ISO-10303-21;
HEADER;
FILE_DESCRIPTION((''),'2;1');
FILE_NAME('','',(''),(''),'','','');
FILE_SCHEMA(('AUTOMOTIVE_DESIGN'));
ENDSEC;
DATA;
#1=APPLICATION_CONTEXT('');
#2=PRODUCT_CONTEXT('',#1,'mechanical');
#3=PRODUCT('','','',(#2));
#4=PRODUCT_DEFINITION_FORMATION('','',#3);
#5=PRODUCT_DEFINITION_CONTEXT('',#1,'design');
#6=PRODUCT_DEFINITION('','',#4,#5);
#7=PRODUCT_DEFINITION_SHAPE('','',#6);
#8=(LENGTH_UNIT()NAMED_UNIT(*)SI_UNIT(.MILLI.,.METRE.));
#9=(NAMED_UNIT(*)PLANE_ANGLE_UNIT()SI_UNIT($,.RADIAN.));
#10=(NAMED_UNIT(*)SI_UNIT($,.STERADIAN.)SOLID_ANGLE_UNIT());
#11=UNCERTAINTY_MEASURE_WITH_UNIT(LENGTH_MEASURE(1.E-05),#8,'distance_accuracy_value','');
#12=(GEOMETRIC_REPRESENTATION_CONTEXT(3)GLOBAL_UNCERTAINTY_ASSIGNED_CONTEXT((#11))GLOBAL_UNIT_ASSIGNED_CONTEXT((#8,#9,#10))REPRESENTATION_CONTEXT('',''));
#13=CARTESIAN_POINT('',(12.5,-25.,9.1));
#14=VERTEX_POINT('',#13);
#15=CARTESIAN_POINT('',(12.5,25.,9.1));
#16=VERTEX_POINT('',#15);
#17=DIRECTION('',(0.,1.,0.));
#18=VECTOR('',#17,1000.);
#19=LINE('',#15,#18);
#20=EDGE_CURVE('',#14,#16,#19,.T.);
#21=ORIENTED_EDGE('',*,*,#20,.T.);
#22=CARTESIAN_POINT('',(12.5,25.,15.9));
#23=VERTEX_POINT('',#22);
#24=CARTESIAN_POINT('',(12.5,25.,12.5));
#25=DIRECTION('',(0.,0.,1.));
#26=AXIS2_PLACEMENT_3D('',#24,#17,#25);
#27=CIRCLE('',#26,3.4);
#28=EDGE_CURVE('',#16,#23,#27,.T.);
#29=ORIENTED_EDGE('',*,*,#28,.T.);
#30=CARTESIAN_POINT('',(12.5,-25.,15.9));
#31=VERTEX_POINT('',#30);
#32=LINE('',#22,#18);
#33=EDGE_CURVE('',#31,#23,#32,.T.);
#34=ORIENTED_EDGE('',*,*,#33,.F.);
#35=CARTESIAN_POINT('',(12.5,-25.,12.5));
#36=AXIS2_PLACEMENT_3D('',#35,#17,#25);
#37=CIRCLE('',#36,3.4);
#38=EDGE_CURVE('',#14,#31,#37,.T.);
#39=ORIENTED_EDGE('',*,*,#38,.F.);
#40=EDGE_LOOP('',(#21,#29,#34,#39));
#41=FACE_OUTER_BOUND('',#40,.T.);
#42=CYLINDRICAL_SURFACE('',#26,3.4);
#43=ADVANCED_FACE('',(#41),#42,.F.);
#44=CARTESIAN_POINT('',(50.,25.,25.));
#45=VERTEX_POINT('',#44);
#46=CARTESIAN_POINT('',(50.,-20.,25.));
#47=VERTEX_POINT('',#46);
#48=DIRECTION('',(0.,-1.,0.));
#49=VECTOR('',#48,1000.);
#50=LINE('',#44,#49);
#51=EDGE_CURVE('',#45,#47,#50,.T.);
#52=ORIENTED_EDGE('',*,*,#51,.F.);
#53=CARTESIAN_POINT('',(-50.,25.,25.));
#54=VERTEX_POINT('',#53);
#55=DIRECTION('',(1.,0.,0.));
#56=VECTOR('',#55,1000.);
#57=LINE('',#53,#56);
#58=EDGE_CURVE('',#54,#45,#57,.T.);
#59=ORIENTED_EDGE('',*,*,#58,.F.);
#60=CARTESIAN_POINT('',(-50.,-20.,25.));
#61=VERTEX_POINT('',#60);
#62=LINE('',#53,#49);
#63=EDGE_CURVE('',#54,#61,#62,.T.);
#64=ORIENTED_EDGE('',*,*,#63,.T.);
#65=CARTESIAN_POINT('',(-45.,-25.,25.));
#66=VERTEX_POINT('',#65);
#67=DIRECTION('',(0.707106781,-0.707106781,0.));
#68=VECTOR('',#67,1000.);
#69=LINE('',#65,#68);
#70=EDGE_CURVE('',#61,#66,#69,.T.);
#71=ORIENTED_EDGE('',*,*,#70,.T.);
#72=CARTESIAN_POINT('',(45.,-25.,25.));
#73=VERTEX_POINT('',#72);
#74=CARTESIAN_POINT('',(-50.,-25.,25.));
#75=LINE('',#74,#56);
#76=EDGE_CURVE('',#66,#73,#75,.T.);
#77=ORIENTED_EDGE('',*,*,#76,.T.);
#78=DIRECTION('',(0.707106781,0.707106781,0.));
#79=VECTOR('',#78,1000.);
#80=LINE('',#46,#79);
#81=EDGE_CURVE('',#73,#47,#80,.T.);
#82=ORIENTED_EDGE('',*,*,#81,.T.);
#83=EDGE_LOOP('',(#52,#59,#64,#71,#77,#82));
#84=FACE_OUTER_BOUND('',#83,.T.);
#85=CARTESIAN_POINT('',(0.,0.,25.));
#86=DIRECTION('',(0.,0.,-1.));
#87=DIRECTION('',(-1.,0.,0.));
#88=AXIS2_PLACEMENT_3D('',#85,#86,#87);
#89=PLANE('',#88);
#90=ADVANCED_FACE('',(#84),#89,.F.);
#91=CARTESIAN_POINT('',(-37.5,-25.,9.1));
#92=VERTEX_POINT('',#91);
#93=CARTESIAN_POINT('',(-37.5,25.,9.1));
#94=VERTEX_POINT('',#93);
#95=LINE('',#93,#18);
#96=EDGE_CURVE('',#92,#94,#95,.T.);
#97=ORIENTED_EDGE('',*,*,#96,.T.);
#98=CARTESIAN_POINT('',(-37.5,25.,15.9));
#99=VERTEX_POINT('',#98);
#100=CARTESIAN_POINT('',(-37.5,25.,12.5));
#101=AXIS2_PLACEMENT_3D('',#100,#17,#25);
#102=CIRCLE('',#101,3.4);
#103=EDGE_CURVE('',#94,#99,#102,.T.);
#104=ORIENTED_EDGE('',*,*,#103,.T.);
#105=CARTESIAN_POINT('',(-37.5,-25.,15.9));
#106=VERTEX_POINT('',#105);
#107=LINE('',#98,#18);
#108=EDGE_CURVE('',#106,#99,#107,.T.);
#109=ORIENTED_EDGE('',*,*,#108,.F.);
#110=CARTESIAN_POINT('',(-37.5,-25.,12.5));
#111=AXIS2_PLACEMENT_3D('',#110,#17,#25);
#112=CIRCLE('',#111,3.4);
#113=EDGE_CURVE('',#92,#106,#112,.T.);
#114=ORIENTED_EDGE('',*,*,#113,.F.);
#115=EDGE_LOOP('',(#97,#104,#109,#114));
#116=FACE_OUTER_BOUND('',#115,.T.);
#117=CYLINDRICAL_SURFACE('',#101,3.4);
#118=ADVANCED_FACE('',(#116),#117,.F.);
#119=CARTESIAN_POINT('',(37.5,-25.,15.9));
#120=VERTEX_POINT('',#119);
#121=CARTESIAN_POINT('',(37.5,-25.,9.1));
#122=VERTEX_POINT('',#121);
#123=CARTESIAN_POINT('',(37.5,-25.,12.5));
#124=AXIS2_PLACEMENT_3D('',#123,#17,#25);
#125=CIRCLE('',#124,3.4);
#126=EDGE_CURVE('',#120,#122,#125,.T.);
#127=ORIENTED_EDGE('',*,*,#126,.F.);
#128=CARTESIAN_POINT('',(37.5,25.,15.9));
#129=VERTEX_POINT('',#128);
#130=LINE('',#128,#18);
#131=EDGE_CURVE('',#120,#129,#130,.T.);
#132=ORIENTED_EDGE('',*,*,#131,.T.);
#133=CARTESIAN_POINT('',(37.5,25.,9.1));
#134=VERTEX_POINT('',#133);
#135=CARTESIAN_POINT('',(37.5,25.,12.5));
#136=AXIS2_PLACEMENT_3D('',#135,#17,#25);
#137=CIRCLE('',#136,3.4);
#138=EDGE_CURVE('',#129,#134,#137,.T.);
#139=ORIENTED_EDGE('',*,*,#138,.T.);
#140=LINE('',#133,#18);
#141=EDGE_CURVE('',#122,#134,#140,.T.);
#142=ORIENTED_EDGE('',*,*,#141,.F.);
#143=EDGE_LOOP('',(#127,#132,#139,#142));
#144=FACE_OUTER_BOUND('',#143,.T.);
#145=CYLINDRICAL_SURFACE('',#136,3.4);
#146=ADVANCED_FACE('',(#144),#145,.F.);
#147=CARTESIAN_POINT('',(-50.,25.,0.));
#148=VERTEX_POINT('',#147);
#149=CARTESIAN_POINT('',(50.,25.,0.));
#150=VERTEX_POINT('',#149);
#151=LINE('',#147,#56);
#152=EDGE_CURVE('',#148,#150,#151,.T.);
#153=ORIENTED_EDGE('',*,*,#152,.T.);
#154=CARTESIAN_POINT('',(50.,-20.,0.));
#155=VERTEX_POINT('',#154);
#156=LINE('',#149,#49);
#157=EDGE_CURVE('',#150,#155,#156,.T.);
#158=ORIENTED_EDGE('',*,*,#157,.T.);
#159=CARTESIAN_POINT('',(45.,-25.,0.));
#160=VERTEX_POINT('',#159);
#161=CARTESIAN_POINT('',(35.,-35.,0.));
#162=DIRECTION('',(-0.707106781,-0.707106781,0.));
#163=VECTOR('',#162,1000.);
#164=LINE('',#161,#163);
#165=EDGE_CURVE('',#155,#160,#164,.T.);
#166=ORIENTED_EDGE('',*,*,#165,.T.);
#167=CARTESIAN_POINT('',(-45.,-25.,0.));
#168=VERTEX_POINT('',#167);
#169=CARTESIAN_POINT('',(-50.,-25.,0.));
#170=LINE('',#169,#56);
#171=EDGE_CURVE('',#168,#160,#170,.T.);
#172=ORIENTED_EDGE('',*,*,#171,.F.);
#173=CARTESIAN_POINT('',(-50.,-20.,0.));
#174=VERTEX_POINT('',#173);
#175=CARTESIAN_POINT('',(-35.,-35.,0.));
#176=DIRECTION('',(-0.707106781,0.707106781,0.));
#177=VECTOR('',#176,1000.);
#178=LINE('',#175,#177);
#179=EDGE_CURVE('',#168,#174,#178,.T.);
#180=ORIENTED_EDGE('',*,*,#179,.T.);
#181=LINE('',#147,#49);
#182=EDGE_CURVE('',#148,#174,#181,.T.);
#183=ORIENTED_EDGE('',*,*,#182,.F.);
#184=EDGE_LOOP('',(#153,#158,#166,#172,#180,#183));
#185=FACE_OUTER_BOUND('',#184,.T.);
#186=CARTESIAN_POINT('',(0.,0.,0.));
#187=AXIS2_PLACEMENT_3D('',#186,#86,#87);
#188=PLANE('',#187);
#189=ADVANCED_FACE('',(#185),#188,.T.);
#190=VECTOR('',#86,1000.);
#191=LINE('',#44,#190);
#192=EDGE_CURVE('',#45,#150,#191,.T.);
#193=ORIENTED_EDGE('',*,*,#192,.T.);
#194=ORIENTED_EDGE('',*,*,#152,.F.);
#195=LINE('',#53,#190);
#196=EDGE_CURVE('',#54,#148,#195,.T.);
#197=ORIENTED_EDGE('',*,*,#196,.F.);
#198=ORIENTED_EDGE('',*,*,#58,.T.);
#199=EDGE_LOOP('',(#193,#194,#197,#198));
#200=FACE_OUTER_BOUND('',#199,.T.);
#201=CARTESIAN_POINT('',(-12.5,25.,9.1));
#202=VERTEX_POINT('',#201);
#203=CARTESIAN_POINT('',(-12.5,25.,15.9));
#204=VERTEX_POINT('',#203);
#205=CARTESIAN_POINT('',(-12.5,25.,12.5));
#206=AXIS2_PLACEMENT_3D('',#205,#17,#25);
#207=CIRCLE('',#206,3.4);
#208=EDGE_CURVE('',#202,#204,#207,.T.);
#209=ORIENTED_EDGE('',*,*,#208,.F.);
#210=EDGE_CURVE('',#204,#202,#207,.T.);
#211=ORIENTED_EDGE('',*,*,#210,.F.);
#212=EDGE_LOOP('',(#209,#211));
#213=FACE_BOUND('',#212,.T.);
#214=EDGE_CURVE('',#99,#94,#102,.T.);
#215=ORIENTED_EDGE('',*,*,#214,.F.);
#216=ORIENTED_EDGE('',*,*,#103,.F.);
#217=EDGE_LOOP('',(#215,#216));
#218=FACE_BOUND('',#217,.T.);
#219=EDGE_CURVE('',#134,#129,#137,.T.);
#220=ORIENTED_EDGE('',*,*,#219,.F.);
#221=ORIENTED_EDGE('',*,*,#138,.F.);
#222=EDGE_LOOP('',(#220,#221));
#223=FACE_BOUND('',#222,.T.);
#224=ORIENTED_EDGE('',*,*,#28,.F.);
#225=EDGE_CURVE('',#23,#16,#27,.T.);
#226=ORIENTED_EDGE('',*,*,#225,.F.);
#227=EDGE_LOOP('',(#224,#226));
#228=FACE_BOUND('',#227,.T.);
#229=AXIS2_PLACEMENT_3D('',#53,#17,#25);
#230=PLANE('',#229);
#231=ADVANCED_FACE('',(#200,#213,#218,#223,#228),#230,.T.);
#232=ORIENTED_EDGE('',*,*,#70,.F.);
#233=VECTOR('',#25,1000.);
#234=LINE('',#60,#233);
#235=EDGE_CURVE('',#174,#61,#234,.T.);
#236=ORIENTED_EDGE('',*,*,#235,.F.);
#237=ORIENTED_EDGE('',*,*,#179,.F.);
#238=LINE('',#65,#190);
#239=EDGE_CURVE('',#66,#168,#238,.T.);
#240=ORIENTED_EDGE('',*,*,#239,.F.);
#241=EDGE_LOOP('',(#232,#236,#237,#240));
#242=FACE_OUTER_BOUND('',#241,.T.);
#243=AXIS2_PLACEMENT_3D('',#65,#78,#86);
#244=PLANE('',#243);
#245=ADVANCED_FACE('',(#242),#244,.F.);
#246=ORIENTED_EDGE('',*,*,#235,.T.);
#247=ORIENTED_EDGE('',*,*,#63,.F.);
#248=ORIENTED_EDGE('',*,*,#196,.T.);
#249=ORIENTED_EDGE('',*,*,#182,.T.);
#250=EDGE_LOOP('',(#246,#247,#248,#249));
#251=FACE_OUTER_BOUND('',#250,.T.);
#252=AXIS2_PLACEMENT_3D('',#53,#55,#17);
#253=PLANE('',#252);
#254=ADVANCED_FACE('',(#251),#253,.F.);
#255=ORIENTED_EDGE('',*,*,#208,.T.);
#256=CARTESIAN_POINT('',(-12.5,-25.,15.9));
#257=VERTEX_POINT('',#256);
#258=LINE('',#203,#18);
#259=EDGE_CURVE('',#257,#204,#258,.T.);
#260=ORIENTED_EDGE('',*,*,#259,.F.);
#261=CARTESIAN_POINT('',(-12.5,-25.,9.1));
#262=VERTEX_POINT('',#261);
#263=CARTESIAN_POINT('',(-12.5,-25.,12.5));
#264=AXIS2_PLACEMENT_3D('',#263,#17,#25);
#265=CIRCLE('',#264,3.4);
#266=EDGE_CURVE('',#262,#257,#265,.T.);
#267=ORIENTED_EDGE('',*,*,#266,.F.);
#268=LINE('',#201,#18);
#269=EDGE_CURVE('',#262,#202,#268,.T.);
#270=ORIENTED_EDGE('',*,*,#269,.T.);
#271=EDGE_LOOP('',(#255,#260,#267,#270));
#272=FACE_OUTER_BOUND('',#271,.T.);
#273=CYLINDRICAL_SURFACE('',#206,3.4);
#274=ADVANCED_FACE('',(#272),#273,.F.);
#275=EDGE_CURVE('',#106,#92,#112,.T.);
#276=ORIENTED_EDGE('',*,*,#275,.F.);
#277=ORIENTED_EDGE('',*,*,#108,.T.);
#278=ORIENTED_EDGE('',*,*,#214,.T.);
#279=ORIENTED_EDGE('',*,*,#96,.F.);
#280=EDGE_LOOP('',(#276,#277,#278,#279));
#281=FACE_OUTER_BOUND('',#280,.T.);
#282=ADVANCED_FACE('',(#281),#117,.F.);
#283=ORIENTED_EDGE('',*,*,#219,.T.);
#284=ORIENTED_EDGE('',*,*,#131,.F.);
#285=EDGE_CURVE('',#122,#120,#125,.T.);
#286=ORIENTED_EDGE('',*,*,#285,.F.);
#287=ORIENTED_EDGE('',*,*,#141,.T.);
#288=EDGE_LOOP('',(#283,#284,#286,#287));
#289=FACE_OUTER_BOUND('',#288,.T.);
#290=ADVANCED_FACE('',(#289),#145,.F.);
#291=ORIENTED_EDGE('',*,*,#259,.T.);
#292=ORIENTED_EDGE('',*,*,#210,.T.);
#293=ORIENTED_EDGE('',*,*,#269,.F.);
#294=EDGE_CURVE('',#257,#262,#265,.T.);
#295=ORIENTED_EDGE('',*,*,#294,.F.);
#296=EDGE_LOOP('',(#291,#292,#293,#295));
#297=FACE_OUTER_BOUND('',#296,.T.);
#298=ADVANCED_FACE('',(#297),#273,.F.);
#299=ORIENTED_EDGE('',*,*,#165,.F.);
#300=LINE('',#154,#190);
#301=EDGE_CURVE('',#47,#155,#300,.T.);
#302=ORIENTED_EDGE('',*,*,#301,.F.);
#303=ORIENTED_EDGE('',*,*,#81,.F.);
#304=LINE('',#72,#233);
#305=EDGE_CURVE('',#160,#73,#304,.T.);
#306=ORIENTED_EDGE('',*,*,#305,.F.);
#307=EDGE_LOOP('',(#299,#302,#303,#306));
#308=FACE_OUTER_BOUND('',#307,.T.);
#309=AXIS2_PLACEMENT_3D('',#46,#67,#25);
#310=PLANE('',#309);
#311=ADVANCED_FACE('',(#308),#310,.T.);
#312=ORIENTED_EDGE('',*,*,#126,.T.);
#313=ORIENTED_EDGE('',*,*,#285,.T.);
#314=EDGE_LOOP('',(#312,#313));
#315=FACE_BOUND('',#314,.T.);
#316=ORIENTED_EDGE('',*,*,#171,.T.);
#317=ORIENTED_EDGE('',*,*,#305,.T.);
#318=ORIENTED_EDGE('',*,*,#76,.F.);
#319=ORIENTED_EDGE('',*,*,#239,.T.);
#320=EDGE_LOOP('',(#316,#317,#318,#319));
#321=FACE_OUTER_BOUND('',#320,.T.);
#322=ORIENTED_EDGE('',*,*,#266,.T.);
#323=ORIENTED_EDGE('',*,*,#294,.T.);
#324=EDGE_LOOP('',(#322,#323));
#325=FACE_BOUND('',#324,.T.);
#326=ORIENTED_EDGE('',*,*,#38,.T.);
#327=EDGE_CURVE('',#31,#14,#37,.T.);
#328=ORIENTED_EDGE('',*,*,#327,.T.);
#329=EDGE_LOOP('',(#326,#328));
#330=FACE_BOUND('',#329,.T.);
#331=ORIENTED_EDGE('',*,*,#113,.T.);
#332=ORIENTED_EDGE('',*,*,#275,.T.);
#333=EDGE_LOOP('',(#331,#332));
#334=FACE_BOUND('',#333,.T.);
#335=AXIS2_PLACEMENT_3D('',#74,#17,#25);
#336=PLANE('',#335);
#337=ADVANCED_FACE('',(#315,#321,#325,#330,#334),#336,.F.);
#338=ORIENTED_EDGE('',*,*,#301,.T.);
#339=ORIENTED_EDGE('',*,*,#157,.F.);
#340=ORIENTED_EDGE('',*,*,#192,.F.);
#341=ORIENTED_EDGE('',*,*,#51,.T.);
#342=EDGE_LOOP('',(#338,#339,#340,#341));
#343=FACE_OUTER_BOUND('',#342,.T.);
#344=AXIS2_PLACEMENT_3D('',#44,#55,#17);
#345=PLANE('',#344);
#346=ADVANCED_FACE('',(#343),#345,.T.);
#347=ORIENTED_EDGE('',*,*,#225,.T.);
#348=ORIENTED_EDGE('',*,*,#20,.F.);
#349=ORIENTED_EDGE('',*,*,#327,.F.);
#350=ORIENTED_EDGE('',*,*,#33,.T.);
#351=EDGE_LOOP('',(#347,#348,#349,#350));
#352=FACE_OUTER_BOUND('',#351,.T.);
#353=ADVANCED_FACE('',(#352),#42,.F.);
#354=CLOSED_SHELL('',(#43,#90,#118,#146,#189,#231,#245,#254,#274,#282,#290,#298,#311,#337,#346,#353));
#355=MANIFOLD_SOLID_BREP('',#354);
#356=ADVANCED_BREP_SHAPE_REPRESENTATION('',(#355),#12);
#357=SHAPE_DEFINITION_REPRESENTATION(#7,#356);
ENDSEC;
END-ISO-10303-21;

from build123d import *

# Parameters (mm, degrees)
SKETCH1_W           = 100
SKETCH1_H           = 50
BOSS_EXTRUDE1_DEPTH = 25
M8_TAPPED_HOLE1_D   = 6.8
CHAMFER1_SIZE       = 5


with BuildPart() as part:
    # Sketch1 → Boss-Extrude1 (new body)
    with BuildSketch(Plane.XY):
        Rectangle(SKETCH1_W, SKETCH1_H)
    extrude(amount=BOSS_EXTRUDE1_DEPTH)

    # M8 Tapped Hole1 (through all)
    with Locations(Plane(origin=(0, 25, 0), x_dir=(1, 0, 0), z_dir=(0, 1, 0))):
        with Locations((-37.5, -12.5), (-12.5, -12.5), (12.5, -12.5), (37.5, -12.5)):
            Hole(M8_TAPPED_HOLE1_D / 2)

    # Chamfer1
    chamfer1_edges = [part.edges().sort_by_distance(p)[0] for p in [
        (-50, -25, 12.5),
        (50, -25, 12.5),
    ]]
    chamfer(chamfer1_edges, length=CHAMFER1_SIZE)


solid = part.part
